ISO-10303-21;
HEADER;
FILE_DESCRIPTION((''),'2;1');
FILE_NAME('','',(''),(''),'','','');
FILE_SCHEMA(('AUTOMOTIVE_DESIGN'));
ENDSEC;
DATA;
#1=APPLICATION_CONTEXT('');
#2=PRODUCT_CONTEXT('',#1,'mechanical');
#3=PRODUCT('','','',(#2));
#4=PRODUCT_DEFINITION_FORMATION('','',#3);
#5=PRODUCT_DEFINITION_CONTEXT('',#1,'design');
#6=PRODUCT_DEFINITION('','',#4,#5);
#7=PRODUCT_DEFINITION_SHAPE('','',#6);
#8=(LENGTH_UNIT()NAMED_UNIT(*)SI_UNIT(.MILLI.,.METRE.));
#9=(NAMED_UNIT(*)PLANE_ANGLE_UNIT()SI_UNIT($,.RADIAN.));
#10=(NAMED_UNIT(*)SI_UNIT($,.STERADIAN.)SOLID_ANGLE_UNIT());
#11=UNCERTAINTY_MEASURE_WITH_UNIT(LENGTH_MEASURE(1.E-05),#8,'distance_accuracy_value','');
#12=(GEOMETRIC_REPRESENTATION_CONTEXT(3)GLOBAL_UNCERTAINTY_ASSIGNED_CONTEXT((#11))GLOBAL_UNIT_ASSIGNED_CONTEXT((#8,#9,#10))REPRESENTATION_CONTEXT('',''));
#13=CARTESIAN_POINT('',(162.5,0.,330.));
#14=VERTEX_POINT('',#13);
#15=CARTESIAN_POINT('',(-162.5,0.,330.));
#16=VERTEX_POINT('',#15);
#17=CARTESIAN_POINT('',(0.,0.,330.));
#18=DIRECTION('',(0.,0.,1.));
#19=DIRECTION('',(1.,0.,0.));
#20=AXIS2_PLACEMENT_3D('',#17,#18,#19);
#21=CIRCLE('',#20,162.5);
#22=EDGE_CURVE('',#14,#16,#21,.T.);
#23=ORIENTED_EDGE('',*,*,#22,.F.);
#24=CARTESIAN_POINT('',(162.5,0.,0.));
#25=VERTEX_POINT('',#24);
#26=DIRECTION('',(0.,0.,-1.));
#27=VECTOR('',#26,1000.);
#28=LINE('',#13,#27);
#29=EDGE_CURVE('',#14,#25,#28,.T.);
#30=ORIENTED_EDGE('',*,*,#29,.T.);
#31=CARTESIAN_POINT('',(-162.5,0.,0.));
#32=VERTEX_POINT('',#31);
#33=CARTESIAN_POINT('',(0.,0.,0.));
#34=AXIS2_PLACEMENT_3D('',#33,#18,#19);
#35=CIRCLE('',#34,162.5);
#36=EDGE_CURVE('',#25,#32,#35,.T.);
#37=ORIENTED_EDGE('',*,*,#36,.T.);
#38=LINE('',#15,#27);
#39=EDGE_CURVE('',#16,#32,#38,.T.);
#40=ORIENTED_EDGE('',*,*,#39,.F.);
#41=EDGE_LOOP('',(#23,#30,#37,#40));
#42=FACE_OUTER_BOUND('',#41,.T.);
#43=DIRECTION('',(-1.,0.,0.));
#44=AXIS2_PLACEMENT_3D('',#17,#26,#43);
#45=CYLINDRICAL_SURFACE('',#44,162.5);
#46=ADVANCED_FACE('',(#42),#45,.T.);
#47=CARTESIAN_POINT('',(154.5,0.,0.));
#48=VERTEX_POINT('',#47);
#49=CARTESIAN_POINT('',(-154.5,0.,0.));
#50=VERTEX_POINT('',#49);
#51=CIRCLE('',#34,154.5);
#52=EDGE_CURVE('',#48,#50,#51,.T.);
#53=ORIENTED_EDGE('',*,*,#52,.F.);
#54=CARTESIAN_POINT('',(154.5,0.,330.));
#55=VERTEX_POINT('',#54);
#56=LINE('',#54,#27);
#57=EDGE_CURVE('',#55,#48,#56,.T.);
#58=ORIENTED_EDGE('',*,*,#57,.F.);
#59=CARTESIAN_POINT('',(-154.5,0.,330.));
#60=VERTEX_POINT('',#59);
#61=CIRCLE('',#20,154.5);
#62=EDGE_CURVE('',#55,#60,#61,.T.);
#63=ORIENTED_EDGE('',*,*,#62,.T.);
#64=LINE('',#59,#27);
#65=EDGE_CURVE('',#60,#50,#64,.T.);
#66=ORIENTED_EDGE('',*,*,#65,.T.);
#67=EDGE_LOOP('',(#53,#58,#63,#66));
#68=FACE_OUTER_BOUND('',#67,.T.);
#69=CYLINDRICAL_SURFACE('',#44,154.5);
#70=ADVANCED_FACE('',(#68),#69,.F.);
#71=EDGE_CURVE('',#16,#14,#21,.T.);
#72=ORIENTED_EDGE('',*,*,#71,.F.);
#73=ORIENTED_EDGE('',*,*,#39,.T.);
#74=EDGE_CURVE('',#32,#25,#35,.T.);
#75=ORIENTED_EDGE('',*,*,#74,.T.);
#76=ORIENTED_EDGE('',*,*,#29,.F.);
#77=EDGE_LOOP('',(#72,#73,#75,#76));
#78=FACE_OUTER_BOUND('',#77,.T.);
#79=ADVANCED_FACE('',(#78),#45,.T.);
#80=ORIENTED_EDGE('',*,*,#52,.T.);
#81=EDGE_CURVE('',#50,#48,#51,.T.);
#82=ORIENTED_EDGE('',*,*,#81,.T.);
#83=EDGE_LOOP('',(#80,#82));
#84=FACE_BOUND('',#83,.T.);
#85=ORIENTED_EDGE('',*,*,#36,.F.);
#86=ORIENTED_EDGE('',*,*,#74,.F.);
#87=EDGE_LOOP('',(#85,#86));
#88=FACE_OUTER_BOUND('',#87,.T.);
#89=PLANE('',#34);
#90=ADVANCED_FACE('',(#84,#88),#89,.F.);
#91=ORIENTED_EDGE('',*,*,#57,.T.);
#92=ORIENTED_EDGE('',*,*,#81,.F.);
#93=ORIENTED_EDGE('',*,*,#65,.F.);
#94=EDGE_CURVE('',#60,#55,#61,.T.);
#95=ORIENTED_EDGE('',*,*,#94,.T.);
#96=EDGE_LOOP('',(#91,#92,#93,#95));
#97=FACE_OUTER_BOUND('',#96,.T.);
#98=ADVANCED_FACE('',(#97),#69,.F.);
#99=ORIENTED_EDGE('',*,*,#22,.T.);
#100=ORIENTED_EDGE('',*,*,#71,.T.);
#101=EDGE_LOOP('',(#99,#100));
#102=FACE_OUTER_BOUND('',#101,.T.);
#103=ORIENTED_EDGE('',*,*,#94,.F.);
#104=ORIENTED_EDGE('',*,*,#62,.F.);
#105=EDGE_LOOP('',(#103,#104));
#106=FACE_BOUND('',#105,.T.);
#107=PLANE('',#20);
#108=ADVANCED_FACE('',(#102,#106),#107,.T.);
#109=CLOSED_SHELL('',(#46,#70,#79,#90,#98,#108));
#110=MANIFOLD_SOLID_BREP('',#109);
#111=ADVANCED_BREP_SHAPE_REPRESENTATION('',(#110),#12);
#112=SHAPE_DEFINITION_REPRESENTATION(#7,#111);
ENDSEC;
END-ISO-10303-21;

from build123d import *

# Parameters (mm, degrees)
SKETCH1_R           = 162.5
SKETCH1_R_2         = 154.5
BOSS_EXTRUDE1_DEPTH = 330


with BuildPart() as part:
    # Sketch1 → Boss-Extrude1 (new body)
    with BuildSketch(Plane.XY):
        Circle(SKETCH1_R)
        Circle(SKETCH1_R_2, mode=Mode.SUBTRACT)
    extrude(amount=BOSS_EXTRUDE1_DEPTH)


solid = part.part
